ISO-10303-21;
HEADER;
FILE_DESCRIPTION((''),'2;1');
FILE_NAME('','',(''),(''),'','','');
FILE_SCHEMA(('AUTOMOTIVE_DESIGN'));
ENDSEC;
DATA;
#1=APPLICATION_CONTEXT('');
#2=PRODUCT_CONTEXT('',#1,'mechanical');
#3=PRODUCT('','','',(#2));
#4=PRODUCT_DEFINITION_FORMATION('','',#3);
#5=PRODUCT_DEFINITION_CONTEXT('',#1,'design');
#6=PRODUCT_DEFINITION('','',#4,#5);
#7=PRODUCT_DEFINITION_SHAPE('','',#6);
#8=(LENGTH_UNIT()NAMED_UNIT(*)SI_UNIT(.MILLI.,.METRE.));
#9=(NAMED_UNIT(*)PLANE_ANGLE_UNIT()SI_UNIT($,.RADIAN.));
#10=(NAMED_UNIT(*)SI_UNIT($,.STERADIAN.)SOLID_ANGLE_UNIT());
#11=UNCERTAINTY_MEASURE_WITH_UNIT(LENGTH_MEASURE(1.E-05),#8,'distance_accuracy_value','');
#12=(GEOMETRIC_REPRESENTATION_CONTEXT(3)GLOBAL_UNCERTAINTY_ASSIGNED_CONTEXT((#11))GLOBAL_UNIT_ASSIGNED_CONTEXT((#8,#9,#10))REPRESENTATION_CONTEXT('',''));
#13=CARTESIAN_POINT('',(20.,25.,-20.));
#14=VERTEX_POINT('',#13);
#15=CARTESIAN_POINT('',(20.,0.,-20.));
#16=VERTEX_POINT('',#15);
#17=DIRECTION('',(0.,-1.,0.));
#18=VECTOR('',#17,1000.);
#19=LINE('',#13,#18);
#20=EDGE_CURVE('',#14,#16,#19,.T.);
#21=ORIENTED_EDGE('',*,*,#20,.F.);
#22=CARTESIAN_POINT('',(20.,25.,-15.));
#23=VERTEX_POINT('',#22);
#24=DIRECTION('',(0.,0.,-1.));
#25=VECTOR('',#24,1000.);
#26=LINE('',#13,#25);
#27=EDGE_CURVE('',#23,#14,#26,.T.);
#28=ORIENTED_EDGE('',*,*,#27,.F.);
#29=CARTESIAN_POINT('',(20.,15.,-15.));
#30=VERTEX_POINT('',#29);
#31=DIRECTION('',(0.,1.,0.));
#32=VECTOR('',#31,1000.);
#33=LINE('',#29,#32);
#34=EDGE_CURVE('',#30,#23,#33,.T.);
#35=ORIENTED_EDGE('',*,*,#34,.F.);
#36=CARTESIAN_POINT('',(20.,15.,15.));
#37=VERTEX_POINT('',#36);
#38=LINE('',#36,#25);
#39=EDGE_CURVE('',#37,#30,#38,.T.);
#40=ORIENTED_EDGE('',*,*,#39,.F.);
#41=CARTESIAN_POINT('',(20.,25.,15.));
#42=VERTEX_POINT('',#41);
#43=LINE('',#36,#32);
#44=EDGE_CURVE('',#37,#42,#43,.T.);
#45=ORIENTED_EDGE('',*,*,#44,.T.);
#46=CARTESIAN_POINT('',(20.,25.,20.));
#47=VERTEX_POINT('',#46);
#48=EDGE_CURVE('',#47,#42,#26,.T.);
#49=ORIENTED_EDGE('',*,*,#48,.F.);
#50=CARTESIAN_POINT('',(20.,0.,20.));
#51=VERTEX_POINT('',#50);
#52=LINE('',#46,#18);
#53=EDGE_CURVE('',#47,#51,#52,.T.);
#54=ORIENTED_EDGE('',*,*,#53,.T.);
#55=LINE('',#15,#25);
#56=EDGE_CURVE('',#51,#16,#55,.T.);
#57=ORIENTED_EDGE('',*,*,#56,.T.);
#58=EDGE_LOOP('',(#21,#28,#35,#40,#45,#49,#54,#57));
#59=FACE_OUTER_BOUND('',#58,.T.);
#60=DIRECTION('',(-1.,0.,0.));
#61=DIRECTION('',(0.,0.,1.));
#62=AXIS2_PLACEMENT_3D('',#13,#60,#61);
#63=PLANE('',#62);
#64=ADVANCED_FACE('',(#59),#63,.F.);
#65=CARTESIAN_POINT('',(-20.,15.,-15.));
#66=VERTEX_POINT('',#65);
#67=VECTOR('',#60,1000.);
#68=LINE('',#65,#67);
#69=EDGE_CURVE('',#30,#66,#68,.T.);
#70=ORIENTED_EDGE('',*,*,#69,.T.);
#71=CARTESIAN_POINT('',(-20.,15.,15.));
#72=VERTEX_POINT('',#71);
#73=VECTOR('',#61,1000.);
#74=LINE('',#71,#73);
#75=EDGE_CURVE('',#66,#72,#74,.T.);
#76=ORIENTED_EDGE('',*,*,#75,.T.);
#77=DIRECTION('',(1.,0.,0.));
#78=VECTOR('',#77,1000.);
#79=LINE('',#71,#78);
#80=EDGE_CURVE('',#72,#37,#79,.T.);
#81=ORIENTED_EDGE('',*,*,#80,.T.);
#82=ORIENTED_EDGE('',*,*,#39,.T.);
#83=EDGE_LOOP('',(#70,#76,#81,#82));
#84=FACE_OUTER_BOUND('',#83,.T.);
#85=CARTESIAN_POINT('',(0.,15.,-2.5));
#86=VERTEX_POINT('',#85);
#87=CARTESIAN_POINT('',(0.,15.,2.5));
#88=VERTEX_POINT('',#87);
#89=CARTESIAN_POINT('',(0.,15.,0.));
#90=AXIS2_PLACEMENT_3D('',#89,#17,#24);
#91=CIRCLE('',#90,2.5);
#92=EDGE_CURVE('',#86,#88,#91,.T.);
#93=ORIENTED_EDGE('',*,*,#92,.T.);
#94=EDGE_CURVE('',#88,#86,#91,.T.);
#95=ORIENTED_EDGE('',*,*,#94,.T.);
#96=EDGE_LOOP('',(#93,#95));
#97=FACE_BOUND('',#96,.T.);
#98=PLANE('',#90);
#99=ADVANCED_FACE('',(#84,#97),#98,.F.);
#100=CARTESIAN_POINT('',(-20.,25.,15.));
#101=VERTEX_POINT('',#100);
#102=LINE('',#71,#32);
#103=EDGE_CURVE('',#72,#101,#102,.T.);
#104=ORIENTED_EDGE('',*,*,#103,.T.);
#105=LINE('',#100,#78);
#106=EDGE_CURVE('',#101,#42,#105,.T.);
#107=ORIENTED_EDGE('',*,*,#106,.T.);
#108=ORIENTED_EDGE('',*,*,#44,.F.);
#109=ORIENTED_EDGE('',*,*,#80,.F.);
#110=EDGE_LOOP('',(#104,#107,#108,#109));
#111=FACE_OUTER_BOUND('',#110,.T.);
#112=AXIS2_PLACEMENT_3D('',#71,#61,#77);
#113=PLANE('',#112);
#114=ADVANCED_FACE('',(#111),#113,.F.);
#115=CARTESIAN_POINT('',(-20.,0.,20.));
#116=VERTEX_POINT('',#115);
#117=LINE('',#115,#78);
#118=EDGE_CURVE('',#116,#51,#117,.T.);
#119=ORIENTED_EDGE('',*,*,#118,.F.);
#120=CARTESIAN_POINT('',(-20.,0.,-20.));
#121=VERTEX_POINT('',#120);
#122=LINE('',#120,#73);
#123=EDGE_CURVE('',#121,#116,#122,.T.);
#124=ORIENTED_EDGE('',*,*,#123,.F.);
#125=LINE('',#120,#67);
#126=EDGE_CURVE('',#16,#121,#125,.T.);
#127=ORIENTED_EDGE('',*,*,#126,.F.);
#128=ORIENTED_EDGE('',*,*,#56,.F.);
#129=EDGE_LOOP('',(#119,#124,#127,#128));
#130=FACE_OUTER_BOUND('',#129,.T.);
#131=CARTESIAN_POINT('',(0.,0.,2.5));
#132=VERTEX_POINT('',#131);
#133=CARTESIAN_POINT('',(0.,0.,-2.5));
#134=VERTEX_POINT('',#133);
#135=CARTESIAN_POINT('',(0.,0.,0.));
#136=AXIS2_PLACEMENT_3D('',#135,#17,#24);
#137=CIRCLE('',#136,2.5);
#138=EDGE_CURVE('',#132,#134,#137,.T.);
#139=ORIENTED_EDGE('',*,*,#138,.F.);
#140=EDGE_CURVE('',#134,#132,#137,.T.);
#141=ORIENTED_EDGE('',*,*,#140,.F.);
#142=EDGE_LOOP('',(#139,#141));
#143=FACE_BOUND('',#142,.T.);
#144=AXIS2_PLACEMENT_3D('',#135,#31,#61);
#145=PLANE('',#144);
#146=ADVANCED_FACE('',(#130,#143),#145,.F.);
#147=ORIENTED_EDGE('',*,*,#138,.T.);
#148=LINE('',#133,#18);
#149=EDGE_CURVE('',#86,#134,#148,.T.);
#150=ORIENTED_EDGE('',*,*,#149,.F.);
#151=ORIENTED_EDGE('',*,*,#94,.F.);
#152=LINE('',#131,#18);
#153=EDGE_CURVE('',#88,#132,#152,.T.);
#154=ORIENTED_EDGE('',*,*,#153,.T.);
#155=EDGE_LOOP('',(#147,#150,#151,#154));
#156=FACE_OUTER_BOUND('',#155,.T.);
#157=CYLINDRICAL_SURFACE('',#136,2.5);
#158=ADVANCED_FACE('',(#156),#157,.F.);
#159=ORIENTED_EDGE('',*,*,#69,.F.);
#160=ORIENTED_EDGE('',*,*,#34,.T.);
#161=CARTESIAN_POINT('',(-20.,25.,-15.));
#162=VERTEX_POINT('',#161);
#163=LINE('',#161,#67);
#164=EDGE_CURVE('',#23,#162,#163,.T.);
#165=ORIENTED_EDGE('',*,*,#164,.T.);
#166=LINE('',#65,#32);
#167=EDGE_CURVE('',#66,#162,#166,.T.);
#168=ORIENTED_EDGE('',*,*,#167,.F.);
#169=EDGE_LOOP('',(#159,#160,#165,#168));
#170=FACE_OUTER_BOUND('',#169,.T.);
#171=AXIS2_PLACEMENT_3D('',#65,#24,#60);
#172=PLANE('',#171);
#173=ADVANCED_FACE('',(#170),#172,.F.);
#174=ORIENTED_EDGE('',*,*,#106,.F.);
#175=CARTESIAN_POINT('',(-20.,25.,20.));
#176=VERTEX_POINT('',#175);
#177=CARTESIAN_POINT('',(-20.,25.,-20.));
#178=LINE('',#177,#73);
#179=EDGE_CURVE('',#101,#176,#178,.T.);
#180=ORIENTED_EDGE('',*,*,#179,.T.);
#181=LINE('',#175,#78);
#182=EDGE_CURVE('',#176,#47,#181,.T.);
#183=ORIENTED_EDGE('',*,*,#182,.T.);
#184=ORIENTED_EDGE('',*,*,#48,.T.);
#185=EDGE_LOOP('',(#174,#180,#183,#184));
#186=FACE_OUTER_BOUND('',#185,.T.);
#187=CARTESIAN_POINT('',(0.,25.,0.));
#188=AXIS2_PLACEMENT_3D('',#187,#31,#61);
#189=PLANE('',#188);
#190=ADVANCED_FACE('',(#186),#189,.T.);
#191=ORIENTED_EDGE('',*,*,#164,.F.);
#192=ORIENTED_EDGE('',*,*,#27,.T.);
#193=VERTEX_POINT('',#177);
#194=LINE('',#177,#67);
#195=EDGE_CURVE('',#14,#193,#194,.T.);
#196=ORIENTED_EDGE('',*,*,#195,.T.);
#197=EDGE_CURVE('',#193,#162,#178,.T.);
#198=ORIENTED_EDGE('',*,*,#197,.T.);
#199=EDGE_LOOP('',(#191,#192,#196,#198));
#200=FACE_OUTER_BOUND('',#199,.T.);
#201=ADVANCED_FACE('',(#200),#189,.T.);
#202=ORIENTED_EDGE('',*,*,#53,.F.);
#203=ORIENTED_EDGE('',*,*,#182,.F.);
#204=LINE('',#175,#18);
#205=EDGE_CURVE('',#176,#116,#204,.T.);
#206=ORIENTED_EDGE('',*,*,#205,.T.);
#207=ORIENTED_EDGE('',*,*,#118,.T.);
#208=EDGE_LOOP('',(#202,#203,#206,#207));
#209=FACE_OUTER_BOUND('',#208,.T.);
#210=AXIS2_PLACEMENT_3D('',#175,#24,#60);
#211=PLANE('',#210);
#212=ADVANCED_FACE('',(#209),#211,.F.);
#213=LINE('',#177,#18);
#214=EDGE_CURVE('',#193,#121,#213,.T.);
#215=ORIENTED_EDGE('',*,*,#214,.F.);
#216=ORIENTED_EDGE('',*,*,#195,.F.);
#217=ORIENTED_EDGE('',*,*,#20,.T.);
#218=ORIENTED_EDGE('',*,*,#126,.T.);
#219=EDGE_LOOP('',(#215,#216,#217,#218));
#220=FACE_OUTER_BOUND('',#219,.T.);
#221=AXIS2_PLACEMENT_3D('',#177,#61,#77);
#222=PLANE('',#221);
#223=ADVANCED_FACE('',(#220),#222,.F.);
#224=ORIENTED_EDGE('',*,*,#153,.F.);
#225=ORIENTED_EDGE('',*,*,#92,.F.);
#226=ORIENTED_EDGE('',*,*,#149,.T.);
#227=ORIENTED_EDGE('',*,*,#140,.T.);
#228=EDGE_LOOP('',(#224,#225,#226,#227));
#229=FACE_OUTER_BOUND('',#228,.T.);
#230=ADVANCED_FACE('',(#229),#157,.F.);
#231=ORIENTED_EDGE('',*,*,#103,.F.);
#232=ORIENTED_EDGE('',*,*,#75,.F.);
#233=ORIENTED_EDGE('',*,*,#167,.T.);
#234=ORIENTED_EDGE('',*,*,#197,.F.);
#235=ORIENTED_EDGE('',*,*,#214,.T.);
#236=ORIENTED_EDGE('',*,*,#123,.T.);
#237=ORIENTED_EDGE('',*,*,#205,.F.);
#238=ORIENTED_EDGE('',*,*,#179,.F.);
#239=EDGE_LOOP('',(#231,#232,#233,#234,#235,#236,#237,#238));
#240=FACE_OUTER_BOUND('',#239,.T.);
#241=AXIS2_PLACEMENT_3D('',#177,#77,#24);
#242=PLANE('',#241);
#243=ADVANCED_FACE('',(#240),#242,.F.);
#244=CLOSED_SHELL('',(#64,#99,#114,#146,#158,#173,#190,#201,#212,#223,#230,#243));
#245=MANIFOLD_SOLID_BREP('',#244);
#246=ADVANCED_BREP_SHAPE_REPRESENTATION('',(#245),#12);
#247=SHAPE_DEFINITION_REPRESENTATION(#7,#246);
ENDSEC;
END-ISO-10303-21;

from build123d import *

# Parameters (mm, degrees)
SKETCH1_W           = 40
SKETCH1_H           = 40
BOSS_EXTRUDE1_DEPTH = 25
SKETCH2_W           = 40
SKETCH2_H           = 30
CUT_EXTRUDE1_DEPTH  = 10
M6_TAPPED_HOLE1_D   = 5


with BuildPart() as part:
    # Sketch1 → Boss-Extrude1 (new body)
    with BuildSketch(Plane(origin=(0, 0, 0), x_dir=(1, 0, 0), z_dir=(0, 1, 0))):
        Rectangle(SKETCH1_W, SKETCH1_H)
    extrude(amount=BOSS_EXTRUDE1_DEPTH)

    # Sketch2 → Cut-Extrude1 (cut)
    with BuildSketch(Plane(origin=(0, 25, 0), x_dir=(1, 0, 0), z_dir=(0, 1, 0))):
        Rectangle(SKETCH2_W, SKETCH2_H)
    extrude(amount=-CUT_EXTRUDE1_DEPTH, mode=Mode.SUBTRACT)

    # M6 Tapped Hole1 (through all)
    with Locations(Plane(origin=(0, 0, 0), x_dir=(-1, 0, 0), z_dir=(0, -1, 0))):
        with Locations((0, 0)):
            Hole(M6_TAPPED_HOLE1_D / 2)


solid = part.part
